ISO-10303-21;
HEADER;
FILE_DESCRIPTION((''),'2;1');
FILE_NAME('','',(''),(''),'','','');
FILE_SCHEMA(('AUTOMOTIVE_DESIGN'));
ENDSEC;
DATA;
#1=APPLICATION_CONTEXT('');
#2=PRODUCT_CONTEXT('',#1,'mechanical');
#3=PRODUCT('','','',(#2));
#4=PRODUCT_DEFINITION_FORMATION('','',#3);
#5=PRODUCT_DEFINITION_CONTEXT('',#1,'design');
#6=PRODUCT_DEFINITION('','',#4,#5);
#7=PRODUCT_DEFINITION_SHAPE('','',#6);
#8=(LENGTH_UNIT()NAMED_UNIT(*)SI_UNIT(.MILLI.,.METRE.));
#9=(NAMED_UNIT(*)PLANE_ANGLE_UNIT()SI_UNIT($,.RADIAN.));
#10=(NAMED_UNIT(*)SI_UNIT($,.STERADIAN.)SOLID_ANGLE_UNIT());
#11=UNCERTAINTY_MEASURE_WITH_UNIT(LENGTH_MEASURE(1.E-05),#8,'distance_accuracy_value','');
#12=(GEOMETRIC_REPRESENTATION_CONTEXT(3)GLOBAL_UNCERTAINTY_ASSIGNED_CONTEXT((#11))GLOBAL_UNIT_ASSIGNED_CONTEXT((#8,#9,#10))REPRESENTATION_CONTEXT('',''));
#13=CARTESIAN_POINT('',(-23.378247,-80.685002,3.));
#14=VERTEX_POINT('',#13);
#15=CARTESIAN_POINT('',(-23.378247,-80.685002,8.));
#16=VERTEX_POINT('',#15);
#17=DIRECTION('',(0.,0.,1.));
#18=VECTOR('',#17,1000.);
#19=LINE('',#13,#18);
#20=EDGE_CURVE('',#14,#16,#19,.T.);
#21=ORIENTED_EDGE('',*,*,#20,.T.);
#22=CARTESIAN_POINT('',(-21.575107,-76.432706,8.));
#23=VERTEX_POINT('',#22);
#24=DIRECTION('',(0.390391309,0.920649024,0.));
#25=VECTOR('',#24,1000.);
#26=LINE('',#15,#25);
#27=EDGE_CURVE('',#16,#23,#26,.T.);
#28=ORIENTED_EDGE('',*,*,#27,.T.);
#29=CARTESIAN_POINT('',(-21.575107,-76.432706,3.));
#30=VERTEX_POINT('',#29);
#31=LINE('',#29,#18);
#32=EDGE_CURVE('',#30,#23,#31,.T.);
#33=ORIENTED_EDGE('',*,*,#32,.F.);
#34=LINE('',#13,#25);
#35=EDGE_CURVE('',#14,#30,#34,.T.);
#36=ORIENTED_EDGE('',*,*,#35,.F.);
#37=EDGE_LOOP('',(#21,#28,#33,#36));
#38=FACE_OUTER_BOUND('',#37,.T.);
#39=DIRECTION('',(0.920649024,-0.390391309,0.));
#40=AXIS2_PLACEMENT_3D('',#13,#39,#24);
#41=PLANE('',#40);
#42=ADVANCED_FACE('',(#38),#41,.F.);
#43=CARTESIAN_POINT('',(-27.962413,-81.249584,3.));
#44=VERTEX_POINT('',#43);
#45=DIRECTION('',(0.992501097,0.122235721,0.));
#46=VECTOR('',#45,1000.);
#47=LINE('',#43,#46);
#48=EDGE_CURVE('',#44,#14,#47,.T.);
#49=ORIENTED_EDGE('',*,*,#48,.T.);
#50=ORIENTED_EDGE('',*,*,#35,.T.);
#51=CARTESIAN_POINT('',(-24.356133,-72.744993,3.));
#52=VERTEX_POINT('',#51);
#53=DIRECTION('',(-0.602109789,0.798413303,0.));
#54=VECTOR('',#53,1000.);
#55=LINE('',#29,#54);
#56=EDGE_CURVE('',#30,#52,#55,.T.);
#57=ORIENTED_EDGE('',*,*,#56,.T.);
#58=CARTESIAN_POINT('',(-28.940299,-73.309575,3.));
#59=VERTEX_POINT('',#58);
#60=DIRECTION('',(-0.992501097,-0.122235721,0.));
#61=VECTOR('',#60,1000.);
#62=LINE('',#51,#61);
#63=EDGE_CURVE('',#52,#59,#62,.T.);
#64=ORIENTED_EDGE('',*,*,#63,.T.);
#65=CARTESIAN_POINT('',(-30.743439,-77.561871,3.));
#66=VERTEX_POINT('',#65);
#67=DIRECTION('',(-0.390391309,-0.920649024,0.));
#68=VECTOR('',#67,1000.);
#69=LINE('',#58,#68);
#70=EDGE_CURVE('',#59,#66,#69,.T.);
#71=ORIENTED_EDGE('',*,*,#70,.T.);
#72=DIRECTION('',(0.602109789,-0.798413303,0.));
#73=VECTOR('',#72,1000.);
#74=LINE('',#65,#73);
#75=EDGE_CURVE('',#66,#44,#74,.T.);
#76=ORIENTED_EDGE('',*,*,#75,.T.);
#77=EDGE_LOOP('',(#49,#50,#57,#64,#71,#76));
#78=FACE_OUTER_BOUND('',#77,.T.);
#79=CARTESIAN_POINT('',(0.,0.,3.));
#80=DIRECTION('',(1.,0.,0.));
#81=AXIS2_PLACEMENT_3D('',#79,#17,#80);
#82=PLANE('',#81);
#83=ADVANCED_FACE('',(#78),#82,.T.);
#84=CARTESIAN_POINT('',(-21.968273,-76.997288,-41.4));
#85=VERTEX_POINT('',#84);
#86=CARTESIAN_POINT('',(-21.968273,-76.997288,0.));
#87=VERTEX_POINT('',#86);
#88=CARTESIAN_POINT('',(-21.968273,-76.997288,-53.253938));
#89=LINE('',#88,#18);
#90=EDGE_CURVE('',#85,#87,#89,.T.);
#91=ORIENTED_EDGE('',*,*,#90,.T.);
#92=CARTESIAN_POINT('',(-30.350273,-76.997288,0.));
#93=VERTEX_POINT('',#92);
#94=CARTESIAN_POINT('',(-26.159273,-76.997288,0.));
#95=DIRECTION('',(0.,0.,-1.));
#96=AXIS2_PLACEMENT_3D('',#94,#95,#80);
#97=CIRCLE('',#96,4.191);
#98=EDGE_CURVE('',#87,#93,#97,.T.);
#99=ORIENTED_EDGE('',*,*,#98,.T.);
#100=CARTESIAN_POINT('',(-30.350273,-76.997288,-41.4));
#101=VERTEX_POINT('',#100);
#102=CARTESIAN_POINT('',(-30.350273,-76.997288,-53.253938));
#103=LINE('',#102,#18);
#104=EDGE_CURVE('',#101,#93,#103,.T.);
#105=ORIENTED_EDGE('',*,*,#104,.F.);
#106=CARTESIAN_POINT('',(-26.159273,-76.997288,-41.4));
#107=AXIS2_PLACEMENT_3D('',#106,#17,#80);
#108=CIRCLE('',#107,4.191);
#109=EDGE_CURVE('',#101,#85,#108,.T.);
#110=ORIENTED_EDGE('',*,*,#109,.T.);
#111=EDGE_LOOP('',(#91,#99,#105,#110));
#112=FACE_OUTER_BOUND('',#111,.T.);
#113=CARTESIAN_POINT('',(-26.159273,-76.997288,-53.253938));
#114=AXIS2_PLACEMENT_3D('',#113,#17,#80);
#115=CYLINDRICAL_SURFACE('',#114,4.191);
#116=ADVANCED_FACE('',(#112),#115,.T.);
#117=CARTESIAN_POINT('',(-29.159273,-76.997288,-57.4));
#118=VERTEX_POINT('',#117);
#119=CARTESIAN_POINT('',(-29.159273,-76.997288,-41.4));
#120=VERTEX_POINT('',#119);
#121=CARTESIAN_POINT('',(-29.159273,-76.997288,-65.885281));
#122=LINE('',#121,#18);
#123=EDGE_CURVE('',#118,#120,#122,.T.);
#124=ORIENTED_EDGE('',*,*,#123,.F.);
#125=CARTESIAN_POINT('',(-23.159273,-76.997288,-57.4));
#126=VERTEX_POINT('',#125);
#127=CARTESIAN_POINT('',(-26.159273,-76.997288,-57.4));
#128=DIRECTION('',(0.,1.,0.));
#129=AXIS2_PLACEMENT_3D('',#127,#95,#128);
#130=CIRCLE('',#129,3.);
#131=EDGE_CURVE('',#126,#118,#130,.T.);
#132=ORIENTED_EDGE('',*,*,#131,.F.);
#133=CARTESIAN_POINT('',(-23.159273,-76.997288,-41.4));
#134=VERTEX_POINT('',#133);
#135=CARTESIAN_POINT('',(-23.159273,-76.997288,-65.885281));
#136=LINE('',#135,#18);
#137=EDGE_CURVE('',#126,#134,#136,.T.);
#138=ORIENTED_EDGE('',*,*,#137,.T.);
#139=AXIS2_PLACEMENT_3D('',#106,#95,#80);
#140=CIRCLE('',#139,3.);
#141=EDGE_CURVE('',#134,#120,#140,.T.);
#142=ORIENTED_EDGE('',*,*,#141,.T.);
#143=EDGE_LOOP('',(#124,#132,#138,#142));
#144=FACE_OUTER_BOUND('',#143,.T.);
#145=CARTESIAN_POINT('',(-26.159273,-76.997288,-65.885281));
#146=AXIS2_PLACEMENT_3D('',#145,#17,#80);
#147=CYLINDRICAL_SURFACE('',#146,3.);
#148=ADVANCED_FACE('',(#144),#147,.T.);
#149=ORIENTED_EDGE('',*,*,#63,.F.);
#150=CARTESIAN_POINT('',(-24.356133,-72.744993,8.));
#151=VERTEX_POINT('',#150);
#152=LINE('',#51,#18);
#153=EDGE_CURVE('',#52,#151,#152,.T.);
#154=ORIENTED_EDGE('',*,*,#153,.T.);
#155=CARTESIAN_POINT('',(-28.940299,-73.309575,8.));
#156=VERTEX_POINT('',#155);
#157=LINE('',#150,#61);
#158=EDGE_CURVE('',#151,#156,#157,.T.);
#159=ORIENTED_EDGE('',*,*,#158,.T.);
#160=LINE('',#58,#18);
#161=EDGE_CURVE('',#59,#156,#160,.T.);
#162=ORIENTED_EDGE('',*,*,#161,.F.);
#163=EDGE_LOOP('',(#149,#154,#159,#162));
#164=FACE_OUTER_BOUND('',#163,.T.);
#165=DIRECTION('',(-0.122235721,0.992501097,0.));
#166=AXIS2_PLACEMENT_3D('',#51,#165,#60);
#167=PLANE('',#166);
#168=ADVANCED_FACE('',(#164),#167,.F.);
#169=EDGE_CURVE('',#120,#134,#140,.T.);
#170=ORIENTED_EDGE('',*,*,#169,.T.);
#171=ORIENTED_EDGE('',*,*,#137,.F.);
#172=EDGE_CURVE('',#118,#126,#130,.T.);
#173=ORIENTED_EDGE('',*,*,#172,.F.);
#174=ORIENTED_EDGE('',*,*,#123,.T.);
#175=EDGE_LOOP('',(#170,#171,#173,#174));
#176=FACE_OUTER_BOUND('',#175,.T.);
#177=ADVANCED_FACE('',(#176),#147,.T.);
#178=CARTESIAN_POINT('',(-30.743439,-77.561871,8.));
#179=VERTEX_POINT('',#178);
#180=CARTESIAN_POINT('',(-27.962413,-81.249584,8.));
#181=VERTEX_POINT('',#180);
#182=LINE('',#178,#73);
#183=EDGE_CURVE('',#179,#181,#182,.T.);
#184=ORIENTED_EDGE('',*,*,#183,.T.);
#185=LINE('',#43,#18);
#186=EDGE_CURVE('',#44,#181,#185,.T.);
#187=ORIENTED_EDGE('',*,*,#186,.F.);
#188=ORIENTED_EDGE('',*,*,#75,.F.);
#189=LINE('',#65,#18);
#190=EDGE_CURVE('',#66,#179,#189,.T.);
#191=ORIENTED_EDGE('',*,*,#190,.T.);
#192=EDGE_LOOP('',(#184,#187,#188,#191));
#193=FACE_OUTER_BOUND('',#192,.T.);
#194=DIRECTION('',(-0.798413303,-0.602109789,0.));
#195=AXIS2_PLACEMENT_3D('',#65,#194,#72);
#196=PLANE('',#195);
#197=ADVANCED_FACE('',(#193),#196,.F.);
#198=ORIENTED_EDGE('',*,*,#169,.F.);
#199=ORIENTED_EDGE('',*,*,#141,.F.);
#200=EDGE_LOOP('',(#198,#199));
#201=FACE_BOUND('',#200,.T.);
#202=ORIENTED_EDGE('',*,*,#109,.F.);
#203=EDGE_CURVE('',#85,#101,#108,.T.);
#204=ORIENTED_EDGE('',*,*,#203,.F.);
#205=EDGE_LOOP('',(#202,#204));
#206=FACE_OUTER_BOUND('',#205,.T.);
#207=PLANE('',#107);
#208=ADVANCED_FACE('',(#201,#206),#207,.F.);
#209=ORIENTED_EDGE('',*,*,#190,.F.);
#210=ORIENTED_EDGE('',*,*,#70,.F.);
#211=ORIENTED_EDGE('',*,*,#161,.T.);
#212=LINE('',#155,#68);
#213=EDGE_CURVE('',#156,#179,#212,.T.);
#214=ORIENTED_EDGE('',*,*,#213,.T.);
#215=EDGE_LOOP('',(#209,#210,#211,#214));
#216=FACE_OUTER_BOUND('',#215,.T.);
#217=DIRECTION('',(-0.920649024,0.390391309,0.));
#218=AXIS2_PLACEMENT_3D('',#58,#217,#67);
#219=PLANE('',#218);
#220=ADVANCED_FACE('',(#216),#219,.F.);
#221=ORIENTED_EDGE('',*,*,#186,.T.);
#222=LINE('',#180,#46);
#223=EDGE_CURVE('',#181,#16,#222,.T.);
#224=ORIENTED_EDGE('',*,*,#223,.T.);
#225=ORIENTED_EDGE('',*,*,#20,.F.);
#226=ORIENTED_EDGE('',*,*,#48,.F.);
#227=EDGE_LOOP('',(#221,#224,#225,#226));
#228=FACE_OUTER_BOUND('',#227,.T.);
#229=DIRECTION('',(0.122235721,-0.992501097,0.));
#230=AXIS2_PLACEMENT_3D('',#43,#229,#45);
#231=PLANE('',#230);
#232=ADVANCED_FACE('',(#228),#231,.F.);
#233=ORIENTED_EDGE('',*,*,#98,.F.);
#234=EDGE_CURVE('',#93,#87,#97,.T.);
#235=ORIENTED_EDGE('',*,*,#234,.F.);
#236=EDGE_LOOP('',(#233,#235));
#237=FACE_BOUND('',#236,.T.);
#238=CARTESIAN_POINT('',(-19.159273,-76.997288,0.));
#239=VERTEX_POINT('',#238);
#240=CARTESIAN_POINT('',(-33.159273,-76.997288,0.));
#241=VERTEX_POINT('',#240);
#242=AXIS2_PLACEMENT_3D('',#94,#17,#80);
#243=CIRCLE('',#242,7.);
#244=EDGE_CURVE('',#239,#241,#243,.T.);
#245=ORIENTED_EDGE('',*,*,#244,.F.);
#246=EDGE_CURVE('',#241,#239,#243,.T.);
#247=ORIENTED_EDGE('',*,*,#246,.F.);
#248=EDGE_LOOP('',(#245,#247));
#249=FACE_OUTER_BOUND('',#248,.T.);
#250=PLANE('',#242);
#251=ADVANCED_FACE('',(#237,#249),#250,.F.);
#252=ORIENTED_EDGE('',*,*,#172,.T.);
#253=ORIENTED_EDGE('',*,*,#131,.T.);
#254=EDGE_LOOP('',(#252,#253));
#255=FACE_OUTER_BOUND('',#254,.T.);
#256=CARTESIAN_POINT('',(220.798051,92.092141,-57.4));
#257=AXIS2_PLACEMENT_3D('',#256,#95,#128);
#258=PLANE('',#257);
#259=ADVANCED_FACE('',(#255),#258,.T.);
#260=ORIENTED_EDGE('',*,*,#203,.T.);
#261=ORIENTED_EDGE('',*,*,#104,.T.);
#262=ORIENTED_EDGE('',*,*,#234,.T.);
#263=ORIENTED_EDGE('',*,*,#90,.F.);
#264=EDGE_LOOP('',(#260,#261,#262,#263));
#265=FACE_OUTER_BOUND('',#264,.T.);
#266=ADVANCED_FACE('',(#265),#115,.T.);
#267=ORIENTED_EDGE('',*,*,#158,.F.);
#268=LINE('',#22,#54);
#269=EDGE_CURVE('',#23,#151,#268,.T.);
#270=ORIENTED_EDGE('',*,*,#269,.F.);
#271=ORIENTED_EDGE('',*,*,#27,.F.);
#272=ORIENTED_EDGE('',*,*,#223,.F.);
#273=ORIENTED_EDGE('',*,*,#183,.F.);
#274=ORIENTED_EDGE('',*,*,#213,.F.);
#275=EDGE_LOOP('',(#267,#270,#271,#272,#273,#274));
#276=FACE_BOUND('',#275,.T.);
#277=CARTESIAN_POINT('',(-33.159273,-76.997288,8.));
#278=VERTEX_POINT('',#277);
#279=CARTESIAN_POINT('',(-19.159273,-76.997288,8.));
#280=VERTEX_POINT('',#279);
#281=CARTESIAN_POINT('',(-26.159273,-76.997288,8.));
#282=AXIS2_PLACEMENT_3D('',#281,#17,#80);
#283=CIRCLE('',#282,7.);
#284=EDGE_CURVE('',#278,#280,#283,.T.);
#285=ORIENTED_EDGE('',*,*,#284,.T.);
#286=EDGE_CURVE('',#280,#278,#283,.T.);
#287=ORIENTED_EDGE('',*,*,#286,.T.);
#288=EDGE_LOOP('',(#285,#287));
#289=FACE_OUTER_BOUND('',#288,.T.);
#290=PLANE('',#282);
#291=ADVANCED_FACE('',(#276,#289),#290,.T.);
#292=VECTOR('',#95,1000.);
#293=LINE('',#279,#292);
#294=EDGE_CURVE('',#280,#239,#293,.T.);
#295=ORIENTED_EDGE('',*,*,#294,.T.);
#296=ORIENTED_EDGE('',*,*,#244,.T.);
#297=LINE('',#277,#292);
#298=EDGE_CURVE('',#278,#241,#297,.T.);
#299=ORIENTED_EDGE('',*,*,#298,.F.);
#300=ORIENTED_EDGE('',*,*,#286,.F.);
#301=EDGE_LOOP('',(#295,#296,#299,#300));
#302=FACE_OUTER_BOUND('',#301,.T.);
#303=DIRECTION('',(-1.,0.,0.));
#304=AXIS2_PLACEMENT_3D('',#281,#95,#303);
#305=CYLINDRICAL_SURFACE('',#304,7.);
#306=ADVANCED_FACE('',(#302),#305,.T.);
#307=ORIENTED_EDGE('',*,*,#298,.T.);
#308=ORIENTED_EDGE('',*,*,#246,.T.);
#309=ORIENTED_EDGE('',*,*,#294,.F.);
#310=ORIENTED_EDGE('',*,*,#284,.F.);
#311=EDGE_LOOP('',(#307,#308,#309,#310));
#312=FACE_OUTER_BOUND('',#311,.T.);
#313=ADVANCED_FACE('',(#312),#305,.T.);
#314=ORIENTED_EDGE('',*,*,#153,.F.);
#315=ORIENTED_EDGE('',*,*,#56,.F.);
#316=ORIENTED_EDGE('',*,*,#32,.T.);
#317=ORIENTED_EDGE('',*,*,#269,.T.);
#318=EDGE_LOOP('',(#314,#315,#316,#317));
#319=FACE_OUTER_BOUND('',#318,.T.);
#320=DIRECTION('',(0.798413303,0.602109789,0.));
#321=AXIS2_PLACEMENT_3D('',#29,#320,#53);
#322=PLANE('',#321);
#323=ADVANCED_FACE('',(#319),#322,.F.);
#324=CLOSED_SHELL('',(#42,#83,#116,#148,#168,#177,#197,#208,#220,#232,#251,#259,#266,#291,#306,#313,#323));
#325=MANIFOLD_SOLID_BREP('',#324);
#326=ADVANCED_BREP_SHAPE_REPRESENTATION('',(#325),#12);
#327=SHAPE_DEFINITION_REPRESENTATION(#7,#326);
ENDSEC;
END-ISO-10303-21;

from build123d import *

# Parameters (mm, degrees)
SKETCH_1_R          = 7
EXTRUDE_1_DEPTH     = 8
SKETCH_2_R          = 4.191
EXTRUDE_2_DEPTH     = 41.4
SKETCH_3_R          = 3
EXTRUDE_3_DEPTH     = 16
CUT_EXTRUDE_1_DEPTH = 5


with BuildPart() as part:
    # 草图1 → 凸台-拉伸1 (new body)
    with BuildSketch(Plane.XY):
        with Locations((-26.159273046, -76.997288483)):
            Circle(SKETCH_1_R)
    extrude(amount=EXTRUDE_1_DEPTH)

    # 草图2 → 凸台-拉伸2 (add)
    with BuildSketch(Plane(origin=(0, 0, 0), x_dir=(-1, 0, 0), z_dir=(0, 0, -1))):
        with Locations(Location((26.159273046, -76.997288483, 0), (0, 0, 180))):
            Circle(SKETCH_2_R)
    extrude(amount=EXTRUDE_2_DEPTH)

    # 草图3 → 凸台-拉伸3 (add)
    with BuildSketch(Plane(origin=(0, 0, -41.4), x_dir=(-1, 0, 0), z_dir=(0, 0, -1))):
        with Locations(Location((26.159273046, -76.997288483, 0), (0, 0, 180))):
            Circle(SKETCH_3_R)
    extrude(amount=EXTRUDE_3_DEPTH)

    # 草图4 → 切除-拉伸1 (cut)
    with BuildSketch(Plane.XY.offset(8)):
        Polygon((-24.356132828, -72.744992787), (-28.940299035, -73.309575399), (-30.743439252, -77.561871096), (-27.962413264, -81.249584179), (-23.378247058, -80.685001566), (-21.57510684, -76.43270587), align=None)
    extrude(amount=-CUT_EXTRUDE_1_DEPTH, mode=Mode.SUBTRACT)


solid = part.part
